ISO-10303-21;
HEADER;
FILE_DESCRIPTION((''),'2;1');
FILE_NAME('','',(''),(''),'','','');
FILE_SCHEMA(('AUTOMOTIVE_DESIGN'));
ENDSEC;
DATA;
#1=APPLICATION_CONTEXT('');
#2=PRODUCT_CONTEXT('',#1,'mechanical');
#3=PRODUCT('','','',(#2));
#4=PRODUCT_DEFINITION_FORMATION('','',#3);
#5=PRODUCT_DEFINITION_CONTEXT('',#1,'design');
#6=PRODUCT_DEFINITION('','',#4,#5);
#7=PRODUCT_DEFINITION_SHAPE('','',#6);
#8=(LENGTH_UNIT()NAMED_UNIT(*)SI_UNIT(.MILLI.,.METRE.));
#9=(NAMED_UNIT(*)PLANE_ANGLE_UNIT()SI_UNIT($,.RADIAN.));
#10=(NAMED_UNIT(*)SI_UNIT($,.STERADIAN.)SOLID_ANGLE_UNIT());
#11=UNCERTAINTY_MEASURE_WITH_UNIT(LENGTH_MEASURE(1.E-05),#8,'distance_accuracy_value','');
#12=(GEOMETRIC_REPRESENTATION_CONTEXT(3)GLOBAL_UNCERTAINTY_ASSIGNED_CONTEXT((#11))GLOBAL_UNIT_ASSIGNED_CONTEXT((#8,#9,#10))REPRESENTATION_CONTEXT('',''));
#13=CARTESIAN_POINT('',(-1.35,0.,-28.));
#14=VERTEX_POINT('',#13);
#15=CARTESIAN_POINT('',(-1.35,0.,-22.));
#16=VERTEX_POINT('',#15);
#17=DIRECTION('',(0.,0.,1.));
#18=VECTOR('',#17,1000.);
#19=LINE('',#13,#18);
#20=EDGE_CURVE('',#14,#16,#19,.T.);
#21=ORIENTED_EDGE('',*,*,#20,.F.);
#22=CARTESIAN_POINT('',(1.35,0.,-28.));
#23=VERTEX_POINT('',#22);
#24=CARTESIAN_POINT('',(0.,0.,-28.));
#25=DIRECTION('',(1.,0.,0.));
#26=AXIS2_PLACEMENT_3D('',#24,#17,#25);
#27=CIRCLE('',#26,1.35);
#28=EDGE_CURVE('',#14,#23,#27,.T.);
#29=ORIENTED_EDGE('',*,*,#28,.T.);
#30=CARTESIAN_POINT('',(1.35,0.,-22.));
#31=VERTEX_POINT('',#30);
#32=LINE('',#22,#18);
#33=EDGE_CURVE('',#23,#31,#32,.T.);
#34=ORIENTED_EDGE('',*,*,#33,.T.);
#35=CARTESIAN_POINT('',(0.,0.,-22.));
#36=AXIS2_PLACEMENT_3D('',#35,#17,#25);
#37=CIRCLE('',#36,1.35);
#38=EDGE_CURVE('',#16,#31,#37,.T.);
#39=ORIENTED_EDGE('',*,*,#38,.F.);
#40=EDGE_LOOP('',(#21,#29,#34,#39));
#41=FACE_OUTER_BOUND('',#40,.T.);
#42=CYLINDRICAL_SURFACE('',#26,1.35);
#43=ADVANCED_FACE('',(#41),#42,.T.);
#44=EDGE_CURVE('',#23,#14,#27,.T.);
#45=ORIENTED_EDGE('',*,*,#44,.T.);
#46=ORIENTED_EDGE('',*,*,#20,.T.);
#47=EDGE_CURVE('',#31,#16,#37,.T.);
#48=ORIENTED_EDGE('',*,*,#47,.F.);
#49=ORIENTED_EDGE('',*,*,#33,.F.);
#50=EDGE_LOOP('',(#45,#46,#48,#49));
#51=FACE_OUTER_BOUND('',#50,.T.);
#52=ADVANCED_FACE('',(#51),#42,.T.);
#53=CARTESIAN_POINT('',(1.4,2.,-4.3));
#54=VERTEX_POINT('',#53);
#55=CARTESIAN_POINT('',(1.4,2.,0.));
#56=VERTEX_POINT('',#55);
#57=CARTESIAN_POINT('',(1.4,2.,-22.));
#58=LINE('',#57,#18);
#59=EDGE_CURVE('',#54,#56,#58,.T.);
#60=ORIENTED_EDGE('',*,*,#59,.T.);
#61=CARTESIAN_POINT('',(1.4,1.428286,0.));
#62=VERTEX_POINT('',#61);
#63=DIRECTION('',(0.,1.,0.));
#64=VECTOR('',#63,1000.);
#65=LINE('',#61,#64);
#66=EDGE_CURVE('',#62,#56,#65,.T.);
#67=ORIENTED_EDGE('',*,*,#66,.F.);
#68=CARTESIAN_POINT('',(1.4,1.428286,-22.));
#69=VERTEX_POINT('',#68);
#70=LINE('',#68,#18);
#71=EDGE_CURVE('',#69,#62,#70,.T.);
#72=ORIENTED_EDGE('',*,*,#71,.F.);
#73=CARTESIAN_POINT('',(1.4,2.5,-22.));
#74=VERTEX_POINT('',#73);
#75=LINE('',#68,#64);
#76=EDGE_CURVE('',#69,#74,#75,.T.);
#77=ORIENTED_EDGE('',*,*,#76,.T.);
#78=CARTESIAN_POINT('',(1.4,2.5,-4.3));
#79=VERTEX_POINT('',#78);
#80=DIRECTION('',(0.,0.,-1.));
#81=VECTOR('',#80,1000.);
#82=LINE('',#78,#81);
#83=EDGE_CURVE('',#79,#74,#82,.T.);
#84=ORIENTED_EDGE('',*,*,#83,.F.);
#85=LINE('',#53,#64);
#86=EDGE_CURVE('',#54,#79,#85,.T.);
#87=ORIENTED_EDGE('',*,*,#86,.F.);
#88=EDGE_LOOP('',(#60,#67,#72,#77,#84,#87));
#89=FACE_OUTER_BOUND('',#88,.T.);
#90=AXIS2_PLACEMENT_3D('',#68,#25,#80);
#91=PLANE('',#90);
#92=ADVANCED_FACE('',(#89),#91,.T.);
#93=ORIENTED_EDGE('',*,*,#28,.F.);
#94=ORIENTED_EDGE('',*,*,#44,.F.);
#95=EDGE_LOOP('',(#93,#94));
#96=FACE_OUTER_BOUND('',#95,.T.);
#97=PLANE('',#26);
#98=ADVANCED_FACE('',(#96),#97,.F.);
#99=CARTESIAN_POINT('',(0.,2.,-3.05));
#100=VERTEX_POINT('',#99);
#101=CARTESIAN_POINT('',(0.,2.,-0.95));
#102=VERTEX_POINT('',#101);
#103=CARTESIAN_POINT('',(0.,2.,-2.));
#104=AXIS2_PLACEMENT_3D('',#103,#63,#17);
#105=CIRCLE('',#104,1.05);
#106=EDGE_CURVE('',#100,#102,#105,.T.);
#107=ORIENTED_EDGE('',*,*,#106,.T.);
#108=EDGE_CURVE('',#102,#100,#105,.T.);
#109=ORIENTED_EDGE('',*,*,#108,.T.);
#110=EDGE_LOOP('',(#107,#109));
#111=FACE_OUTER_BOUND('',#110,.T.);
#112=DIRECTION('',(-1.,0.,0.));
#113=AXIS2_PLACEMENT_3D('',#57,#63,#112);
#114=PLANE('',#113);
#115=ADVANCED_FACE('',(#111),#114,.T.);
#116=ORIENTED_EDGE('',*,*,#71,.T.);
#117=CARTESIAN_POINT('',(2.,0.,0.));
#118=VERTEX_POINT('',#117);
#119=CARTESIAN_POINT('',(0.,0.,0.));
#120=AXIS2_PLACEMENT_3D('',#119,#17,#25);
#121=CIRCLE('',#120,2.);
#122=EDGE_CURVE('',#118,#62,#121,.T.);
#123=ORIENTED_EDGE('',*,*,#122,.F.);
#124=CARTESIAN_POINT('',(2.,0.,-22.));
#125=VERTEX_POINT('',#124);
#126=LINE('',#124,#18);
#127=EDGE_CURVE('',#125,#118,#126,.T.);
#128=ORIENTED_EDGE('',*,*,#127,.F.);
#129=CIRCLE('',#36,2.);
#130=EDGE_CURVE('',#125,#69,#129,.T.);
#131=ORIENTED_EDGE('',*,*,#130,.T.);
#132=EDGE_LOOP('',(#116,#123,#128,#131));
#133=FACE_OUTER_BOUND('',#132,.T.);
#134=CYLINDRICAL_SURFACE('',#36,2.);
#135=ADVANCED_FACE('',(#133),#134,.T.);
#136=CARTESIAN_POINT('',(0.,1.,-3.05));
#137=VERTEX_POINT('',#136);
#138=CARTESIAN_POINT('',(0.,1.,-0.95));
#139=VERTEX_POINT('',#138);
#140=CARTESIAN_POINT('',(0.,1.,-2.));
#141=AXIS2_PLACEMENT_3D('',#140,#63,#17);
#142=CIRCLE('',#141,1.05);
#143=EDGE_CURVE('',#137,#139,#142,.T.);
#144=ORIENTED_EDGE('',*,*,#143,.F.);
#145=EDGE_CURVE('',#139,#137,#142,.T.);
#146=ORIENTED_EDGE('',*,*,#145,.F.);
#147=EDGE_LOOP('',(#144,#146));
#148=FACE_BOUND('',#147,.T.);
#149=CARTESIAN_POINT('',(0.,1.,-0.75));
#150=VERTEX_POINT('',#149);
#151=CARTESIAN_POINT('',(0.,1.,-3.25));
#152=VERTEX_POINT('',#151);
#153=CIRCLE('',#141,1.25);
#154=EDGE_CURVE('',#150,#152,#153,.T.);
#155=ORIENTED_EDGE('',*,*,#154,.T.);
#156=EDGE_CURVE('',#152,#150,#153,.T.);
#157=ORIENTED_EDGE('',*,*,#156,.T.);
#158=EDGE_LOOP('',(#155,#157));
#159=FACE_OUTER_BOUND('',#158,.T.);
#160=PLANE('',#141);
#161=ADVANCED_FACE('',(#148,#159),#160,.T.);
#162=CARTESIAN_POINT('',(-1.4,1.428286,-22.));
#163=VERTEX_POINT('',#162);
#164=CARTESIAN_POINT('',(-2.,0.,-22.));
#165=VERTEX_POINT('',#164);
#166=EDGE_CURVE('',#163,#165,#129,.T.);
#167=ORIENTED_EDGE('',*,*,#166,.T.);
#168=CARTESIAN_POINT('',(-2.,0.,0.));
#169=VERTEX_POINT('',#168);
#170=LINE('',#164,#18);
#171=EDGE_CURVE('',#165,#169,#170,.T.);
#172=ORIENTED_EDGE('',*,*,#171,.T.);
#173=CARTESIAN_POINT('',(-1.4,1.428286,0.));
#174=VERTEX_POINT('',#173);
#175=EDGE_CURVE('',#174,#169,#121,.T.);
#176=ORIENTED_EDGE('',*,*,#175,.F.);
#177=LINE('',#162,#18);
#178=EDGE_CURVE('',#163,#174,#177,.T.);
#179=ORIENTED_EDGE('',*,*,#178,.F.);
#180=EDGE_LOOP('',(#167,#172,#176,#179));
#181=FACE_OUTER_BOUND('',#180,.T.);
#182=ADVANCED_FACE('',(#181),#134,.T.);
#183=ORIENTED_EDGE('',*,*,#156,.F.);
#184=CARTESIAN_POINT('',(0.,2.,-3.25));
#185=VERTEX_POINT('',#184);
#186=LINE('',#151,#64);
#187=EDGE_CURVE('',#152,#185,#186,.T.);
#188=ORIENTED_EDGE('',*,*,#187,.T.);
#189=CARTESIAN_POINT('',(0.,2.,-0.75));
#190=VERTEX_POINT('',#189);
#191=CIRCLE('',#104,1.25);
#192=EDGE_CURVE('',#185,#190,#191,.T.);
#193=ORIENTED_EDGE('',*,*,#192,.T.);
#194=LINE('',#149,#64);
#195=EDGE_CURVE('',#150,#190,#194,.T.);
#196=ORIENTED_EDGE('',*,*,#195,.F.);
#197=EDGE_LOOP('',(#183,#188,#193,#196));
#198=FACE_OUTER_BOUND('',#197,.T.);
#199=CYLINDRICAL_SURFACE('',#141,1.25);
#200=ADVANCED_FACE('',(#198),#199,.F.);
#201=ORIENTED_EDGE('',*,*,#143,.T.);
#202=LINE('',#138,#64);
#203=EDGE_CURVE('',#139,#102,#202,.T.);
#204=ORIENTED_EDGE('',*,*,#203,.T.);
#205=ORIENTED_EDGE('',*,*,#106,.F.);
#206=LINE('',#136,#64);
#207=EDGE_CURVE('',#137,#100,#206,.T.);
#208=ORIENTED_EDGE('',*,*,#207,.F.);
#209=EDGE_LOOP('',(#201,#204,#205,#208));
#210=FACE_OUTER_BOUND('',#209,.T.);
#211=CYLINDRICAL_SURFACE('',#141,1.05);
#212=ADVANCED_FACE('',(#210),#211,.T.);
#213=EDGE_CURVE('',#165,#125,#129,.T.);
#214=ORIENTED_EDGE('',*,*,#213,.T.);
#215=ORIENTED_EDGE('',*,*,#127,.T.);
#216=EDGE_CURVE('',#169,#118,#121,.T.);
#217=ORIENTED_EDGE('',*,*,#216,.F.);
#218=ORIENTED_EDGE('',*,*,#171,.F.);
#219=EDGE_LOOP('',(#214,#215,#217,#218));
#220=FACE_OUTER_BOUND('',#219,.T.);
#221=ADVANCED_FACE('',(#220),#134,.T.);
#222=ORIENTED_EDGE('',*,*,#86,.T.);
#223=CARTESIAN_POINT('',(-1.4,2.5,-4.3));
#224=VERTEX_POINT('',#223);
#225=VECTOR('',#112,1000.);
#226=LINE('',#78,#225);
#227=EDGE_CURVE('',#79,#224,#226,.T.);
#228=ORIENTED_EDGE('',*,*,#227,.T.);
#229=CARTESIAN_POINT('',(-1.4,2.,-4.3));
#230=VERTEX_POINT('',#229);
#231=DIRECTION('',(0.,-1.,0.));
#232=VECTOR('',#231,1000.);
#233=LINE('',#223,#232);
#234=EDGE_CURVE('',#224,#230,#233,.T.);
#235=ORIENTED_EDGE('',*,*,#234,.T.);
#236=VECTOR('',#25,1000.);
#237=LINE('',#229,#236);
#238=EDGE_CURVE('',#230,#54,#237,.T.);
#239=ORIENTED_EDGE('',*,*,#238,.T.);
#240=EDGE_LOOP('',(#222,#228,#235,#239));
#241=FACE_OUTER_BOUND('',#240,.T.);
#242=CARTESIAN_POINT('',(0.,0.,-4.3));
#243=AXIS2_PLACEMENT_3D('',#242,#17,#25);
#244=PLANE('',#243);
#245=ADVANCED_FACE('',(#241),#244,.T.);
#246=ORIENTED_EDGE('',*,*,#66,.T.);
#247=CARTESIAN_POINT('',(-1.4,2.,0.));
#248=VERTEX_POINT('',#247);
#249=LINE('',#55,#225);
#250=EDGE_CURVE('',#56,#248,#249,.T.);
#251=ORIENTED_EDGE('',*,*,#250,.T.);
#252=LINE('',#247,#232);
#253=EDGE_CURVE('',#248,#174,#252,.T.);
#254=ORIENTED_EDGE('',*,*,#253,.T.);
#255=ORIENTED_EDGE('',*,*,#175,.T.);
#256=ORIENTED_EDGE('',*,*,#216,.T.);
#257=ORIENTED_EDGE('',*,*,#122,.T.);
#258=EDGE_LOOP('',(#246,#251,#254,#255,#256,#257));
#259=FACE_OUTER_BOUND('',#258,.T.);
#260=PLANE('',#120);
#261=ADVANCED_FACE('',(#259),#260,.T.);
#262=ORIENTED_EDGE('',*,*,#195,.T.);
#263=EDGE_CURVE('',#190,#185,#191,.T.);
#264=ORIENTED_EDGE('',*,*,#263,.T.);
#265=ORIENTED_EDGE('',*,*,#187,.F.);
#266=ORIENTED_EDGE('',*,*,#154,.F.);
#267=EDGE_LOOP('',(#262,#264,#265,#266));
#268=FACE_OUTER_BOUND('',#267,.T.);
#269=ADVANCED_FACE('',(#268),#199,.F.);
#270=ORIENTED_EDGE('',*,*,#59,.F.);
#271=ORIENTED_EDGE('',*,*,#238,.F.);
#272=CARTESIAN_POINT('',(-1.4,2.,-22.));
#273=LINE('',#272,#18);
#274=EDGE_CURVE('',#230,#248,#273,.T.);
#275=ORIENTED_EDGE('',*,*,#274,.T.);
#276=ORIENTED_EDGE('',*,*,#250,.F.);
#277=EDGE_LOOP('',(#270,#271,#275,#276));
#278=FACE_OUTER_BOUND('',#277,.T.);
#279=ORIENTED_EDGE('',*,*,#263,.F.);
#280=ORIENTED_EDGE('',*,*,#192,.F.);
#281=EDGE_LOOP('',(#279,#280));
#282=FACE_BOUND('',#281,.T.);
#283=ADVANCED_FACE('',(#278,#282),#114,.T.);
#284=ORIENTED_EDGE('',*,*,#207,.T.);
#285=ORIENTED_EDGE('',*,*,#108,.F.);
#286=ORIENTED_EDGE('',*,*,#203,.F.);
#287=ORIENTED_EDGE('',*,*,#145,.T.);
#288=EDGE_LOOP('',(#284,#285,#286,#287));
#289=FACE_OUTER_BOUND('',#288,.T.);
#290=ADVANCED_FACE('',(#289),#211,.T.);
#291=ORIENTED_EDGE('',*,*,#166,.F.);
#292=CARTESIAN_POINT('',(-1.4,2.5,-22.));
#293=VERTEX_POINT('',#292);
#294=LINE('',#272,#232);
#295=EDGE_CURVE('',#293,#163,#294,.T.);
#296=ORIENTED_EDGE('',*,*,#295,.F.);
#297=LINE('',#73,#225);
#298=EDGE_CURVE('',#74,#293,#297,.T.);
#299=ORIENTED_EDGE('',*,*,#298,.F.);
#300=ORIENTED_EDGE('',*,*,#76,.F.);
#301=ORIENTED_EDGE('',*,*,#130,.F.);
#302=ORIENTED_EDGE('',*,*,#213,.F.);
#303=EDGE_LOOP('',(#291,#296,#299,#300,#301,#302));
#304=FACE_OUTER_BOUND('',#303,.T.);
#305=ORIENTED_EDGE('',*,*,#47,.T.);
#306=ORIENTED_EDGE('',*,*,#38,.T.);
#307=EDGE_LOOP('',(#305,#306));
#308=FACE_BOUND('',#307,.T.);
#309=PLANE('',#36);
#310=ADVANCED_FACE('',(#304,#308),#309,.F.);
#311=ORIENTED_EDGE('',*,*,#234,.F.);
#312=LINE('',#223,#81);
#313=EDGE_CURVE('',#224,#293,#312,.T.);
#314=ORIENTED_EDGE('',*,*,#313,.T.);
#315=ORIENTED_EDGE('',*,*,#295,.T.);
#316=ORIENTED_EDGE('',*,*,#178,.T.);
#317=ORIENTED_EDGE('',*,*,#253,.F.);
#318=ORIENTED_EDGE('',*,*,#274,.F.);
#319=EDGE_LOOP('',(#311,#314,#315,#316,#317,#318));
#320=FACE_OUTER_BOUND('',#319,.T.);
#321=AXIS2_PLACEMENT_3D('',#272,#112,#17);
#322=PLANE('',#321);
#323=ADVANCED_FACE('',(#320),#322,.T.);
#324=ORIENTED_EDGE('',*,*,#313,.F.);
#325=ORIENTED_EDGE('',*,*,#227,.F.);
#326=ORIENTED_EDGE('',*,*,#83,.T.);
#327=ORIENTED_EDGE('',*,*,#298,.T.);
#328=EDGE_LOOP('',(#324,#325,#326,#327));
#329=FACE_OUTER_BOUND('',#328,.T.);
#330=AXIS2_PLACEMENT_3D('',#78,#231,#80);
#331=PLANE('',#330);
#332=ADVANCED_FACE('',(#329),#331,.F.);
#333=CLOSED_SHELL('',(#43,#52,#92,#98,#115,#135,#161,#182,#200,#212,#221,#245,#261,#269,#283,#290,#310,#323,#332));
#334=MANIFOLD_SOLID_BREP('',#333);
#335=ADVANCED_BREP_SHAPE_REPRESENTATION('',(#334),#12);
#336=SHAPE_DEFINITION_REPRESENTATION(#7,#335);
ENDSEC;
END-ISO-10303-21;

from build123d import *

# Parameters (mm, degrees)
BOSS_EXTRUDE1_DEPTH = 22
SKETCH2_W           = 2.8
SKETCH2_H           = 0.5
BOSS_EXTRUDE2_DEPTH = 17.7
SKETCH3_R           = 1.25
SKETCH3_R_2         = 1.05
CUT_EXTRUDE1_DEPTH  = 1
SKETCH4_R           = 1.35
BOSS_EXTRUDE3_DEPTH = 6


with BuildPart() as part:
    # Sketch1 → Boss-Extrude1 (new body)
    with BuildSketch(Plane.XY):
        with BuildLine():
            Line((1.4, 1.428285686), (1.4, 2))
            Line((1.4, 2), (-1.4, 2))
            Line((-1.4, 2), (-1.4, 1.428285686))
            ThreePointArc((-1.4, 1.428285686), (0, -2), (1.4, 1.428285686))
        make_face()
    extrude(amount=-BOSS_EXTRUDE1_DEPTH)

    # Sketch2 → Boss-Extrude2 (add)
    with BuildSketch(Plane.XY.offset(-22)):
        with Locations((0, 2.25)):
            Rectangle(SKETCH2_W, SKETCH2_H)
    extrude(amount=BOSS_EXTRUDE2_DEPTH)

    # Sketch3 → Cut-Extrude1 (cut)
    with BuildSketch(Plane(origin=(0, 2, 0), x_dir=(1, 0, 0), z_dir=(0, 1, 0))):
        with Locations(Location((0, 2, 0), (0, 0, 270))):
            Circle(SKETCH3_R)
        with Locations(Location((0, 2, 0), (0, 0, 270))):
            Circle(SKETCH3_R_2, mode=Mode.SUBTRACT)
    extrude(amount=-CUT_EXTRUDE1_DEPTH, mode=Mode.SUBTRACT)

    # Sketch4 → Boss-Extrude3 (add)
    with BuildSketch(Plane.XY.offset(-22)):
        Circle(SKETCH4_R)
    extrude(amount=-BOSS_EXTRUDE3_DEPTH)


solid = part.part
